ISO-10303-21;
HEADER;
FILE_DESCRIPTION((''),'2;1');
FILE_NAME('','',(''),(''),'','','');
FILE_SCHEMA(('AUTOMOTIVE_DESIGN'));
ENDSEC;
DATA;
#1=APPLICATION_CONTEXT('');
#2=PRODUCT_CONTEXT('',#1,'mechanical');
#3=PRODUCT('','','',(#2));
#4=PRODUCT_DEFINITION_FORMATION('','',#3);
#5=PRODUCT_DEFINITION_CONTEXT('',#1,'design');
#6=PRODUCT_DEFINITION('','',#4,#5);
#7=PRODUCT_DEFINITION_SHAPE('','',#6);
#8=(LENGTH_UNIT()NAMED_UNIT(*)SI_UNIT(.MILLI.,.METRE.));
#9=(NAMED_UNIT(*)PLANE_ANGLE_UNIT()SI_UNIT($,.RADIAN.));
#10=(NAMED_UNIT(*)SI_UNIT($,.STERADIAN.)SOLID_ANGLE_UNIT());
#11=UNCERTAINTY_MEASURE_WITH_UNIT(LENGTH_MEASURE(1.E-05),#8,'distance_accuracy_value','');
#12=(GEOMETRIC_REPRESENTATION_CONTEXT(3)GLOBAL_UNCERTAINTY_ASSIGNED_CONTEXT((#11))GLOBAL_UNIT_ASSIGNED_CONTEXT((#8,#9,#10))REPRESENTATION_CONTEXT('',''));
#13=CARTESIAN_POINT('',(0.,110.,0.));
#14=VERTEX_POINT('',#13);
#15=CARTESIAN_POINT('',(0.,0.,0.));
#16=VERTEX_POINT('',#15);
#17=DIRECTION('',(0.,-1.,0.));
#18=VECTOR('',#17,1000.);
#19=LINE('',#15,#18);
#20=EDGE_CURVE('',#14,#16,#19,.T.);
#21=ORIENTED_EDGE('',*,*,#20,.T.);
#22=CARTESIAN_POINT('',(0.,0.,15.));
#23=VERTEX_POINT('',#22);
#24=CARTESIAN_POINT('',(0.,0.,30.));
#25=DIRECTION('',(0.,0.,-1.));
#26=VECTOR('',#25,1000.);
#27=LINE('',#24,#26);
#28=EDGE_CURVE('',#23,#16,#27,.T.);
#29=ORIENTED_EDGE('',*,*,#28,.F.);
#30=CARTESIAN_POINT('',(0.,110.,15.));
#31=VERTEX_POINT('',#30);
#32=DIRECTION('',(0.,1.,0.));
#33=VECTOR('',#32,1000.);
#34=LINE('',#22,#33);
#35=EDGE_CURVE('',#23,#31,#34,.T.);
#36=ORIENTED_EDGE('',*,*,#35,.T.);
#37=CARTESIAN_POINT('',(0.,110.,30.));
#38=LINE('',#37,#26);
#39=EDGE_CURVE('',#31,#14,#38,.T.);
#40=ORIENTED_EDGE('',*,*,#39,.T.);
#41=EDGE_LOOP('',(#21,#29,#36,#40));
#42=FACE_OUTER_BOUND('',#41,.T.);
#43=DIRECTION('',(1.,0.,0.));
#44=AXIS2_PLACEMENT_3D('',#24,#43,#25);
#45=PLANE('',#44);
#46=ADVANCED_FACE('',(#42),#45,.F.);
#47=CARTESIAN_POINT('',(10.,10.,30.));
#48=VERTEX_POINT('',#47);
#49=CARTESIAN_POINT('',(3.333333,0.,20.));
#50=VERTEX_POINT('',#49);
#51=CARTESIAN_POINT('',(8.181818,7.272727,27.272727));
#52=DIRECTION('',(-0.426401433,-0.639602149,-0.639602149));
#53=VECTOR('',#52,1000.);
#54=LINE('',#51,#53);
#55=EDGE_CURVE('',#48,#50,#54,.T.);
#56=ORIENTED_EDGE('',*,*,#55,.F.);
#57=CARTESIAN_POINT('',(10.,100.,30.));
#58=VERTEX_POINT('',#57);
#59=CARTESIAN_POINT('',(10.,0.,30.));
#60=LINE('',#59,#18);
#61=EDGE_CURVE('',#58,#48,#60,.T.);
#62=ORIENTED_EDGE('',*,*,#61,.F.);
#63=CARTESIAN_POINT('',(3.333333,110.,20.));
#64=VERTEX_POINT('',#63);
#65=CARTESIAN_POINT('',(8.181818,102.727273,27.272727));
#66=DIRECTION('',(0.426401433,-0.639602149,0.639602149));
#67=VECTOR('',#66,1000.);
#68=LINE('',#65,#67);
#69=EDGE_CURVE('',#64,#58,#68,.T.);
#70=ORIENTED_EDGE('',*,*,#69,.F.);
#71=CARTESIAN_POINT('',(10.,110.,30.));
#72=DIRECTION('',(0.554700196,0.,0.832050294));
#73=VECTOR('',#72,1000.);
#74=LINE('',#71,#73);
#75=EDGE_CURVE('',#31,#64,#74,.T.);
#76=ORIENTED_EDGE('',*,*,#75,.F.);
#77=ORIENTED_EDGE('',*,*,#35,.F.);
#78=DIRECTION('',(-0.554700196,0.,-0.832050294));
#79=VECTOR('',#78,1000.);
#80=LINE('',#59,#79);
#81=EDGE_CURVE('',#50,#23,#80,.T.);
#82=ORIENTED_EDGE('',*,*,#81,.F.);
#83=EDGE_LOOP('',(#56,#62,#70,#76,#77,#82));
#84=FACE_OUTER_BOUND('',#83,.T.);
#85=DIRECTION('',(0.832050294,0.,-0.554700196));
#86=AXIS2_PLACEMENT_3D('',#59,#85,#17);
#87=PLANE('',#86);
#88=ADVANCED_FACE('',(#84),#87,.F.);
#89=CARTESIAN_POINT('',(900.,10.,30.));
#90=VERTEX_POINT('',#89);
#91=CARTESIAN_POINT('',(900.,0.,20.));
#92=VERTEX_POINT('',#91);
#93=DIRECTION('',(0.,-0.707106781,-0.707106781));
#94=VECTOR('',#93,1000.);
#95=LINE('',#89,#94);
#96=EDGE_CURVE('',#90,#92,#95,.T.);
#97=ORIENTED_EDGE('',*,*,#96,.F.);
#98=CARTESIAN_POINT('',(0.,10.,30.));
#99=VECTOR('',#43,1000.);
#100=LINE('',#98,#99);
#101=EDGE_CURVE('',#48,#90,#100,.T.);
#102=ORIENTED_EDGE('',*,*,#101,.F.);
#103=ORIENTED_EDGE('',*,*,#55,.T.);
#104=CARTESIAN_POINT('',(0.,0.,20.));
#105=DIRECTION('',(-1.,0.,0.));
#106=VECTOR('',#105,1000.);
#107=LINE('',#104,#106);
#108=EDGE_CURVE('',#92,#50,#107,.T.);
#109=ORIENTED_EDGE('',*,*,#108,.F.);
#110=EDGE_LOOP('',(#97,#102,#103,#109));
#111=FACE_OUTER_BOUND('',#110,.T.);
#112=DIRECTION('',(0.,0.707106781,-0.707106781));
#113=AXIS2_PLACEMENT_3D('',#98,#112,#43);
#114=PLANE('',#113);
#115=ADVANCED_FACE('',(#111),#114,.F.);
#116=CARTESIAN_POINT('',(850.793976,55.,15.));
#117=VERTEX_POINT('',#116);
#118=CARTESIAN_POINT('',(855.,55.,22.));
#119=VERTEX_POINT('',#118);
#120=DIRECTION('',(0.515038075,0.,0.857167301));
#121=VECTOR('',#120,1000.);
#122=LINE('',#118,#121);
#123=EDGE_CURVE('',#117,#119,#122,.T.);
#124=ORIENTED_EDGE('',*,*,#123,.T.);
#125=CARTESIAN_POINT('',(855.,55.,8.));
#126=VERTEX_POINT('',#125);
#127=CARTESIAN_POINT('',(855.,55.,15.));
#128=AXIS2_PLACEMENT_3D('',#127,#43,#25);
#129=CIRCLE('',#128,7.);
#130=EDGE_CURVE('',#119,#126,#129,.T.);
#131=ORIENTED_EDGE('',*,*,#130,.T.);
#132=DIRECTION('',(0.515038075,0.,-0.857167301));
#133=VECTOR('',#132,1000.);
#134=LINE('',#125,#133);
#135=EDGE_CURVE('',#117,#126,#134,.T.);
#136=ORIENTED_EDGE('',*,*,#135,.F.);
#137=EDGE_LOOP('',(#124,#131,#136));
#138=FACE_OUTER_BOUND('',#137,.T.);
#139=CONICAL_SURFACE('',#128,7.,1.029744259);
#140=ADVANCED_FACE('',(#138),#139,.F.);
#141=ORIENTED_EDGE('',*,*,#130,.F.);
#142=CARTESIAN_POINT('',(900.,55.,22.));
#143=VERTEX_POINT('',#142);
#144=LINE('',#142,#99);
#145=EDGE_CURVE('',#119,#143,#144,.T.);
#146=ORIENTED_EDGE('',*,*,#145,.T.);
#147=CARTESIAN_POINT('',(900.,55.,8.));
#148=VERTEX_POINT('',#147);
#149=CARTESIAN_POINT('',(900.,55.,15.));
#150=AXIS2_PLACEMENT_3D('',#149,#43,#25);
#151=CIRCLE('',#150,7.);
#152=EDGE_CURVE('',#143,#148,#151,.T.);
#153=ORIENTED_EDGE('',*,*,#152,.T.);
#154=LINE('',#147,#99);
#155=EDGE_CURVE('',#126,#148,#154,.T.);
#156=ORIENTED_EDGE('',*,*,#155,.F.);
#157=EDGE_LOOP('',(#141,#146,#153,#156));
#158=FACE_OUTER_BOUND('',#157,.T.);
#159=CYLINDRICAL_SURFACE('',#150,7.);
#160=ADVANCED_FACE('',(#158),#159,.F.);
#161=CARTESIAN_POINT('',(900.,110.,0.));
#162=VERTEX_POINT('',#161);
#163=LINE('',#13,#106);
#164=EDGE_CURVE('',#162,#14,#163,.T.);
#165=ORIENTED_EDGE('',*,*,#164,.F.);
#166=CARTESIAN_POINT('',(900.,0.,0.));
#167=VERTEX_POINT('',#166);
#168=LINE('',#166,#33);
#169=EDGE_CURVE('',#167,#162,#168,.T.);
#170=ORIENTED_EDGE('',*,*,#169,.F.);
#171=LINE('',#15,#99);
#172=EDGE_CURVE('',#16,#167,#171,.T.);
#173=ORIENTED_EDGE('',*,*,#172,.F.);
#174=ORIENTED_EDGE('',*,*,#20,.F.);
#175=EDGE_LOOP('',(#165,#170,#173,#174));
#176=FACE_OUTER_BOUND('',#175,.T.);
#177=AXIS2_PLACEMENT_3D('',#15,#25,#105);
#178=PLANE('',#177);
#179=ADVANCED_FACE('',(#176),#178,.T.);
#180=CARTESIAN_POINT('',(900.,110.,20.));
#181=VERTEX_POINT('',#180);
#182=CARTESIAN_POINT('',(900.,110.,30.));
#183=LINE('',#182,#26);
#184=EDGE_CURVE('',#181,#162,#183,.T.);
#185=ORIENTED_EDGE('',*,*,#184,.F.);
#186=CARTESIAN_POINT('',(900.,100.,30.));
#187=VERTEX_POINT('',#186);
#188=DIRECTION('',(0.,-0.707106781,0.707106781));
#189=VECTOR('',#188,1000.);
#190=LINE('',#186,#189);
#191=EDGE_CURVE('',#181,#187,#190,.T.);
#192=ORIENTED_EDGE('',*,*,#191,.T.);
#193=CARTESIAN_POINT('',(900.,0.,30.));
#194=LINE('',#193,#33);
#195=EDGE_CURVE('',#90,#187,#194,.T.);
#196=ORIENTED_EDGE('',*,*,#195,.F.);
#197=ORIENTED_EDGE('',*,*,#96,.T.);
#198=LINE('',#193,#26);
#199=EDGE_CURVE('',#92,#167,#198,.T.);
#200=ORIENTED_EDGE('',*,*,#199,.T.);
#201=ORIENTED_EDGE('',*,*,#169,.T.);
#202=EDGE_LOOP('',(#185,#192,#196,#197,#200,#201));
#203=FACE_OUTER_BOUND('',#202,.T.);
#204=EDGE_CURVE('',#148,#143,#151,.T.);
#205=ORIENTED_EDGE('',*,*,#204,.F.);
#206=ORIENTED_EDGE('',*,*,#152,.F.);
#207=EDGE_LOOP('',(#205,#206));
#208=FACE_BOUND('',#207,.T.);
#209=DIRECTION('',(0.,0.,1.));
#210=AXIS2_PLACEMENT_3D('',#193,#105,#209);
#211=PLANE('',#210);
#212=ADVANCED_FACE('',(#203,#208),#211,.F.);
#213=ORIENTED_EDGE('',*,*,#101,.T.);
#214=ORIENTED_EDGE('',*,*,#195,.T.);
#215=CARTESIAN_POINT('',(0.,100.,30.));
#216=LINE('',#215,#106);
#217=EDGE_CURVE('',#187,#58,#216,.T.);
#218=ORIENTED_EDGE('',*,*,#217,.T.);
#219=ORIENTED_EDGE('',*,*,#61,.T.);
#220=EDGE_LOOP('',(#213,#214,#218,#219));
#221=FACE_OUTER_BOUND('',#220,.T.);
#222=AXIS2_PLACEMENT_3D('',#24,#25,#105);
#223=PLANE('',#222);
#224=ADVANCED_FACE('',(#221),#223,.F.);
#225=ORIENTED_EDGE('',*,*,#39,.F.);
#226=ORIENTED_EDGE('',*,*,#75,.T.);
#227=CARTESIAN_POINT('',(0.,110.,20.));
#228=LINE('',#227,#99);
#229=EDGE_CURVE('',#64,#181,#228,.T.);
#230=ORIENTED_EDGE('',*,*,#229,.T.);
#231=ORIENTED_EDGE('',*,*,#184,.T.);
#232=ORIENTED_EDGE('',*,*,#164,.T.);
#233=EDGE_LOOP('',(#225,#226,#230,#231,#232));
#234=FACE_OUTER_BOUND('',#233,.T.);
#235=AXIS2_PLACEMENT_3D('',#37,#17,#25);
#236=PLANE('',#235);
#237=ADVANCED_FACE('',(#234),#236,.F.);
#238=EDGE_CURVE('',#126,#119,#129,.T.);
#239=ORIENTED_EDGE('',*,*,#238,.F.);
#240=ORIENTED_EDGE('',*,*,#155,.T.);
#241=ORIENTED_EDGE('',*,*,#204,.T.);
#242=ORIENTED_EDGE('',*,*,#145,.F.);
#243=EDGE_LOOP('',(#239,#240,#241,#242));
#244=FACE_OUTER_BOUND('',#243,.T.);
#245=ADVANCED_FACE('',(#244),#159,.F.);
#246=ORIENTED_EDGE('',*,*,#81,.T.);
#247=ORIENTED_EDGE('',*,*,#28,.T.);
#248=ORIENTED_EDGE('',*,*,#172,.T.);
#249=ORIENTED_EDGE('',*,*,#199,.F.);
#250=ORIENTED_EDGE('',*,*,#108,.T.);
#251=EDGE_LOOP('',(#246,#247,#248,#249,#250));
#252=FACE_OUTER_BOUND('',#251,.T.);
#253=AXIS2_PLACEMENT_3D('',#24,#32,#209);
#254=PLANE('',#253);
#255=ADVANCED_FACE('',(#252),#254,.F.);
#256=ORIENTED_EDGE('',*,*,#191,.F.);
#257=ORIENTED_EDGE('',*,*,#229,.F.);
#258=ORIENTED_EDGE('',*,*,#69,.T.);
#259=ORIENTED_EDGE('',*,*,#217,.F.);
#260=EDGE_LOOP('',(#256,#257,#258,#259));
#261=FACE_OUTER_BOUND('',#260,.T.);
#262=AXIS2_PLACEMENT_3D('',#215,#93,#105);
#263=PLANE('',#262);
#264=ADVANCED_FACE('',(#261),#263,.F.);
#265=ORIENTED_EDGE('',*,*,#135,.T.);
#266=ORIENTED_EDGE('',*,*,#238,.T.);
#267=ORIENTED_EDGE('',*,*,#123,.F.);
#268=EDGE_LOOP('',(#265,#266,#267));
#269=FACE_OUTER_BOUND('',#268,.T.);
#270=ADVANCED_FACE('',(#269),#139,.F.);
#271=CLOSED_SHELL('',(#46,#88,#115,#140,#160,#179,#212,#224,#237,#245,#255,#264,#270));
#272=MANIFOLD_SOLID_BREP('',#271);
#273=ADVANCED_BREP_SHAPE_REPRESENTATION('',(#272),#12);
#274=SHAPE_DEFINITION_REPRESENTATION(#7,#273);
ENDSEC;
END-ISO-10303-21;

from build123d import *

# Parameters (mm, degrees)
SKETCH1_W              = 900
SKETCH1_H              = 110
BOSS_EXTRUDE1_DEPTH    = 30
CHAMFER1_SIZE          = 10
CHAMFER2_SIZE          = 15
CHAMFER2_SIZE2         = 10
M16_TAPPED_HOLE1_D     = 14
M16_TAPPED_HOLE1_DEPTH = 45
M16_TAPPED_HOLE1_TIP   = 4.206024333


with BuildPart() as part:
    # Sketch1 → Boss-Extrude1 (new body)
    with BuildSketch(Plane.XY):
        with Locations((450, 55)):
            Rectangle(SKETCH1_W, SKETCH1_H)
    extrude(amount=BOSS_EXTRUDE1_DEPTH)

    # Chamfer1
    chamfer1_edges = [part.edges().sort_by_distance(p)[0] for p in [
        (450, 110, 30),
        (450, 0, 30),
    ]]
    chamfer(chamfer1_edges, length=CHAMFER1_SIZE)

    # Chamfer2
    chamfer2_edges = [part.edges().sort_by_distance(p)[0] for p in [
        (0, 55, 30),
    ]]
    chamfer2_side = [part.faces().sort_by_distance(p)[0] for p in [
        (0, 55, 14.635416667),
    ]]
    chamfer(chamfer2_edges, length=CHAMFER2_SIZE, length2=CHAMFER2_SIZE2, reference=chamfer2_side[0])

    # M16 Tapped Hole1
    with Locations(Plane(origin=(900, 55, 15), x_dir=(0, 0, 1), z_dir=(1, 0, 0))):
        with Locations((0, 0)):
            Hole(M16_TAPPED_HOLE1_D / 2, depth=M16_TAPPED_HOLE1_DEPTH)
            with Locations((0, 0, -(M16_TAPPED_HOLE1_DEPTH + M16_TAPPED_HOLE1_TIP / 2))):  # 118° drill point
                Cone(0, M16_TAPPED_HOLE1_D / 2, M16_TAPPED_HOLE1_TIP, mode=Mode.SUBTRACT)


solid = part.part
